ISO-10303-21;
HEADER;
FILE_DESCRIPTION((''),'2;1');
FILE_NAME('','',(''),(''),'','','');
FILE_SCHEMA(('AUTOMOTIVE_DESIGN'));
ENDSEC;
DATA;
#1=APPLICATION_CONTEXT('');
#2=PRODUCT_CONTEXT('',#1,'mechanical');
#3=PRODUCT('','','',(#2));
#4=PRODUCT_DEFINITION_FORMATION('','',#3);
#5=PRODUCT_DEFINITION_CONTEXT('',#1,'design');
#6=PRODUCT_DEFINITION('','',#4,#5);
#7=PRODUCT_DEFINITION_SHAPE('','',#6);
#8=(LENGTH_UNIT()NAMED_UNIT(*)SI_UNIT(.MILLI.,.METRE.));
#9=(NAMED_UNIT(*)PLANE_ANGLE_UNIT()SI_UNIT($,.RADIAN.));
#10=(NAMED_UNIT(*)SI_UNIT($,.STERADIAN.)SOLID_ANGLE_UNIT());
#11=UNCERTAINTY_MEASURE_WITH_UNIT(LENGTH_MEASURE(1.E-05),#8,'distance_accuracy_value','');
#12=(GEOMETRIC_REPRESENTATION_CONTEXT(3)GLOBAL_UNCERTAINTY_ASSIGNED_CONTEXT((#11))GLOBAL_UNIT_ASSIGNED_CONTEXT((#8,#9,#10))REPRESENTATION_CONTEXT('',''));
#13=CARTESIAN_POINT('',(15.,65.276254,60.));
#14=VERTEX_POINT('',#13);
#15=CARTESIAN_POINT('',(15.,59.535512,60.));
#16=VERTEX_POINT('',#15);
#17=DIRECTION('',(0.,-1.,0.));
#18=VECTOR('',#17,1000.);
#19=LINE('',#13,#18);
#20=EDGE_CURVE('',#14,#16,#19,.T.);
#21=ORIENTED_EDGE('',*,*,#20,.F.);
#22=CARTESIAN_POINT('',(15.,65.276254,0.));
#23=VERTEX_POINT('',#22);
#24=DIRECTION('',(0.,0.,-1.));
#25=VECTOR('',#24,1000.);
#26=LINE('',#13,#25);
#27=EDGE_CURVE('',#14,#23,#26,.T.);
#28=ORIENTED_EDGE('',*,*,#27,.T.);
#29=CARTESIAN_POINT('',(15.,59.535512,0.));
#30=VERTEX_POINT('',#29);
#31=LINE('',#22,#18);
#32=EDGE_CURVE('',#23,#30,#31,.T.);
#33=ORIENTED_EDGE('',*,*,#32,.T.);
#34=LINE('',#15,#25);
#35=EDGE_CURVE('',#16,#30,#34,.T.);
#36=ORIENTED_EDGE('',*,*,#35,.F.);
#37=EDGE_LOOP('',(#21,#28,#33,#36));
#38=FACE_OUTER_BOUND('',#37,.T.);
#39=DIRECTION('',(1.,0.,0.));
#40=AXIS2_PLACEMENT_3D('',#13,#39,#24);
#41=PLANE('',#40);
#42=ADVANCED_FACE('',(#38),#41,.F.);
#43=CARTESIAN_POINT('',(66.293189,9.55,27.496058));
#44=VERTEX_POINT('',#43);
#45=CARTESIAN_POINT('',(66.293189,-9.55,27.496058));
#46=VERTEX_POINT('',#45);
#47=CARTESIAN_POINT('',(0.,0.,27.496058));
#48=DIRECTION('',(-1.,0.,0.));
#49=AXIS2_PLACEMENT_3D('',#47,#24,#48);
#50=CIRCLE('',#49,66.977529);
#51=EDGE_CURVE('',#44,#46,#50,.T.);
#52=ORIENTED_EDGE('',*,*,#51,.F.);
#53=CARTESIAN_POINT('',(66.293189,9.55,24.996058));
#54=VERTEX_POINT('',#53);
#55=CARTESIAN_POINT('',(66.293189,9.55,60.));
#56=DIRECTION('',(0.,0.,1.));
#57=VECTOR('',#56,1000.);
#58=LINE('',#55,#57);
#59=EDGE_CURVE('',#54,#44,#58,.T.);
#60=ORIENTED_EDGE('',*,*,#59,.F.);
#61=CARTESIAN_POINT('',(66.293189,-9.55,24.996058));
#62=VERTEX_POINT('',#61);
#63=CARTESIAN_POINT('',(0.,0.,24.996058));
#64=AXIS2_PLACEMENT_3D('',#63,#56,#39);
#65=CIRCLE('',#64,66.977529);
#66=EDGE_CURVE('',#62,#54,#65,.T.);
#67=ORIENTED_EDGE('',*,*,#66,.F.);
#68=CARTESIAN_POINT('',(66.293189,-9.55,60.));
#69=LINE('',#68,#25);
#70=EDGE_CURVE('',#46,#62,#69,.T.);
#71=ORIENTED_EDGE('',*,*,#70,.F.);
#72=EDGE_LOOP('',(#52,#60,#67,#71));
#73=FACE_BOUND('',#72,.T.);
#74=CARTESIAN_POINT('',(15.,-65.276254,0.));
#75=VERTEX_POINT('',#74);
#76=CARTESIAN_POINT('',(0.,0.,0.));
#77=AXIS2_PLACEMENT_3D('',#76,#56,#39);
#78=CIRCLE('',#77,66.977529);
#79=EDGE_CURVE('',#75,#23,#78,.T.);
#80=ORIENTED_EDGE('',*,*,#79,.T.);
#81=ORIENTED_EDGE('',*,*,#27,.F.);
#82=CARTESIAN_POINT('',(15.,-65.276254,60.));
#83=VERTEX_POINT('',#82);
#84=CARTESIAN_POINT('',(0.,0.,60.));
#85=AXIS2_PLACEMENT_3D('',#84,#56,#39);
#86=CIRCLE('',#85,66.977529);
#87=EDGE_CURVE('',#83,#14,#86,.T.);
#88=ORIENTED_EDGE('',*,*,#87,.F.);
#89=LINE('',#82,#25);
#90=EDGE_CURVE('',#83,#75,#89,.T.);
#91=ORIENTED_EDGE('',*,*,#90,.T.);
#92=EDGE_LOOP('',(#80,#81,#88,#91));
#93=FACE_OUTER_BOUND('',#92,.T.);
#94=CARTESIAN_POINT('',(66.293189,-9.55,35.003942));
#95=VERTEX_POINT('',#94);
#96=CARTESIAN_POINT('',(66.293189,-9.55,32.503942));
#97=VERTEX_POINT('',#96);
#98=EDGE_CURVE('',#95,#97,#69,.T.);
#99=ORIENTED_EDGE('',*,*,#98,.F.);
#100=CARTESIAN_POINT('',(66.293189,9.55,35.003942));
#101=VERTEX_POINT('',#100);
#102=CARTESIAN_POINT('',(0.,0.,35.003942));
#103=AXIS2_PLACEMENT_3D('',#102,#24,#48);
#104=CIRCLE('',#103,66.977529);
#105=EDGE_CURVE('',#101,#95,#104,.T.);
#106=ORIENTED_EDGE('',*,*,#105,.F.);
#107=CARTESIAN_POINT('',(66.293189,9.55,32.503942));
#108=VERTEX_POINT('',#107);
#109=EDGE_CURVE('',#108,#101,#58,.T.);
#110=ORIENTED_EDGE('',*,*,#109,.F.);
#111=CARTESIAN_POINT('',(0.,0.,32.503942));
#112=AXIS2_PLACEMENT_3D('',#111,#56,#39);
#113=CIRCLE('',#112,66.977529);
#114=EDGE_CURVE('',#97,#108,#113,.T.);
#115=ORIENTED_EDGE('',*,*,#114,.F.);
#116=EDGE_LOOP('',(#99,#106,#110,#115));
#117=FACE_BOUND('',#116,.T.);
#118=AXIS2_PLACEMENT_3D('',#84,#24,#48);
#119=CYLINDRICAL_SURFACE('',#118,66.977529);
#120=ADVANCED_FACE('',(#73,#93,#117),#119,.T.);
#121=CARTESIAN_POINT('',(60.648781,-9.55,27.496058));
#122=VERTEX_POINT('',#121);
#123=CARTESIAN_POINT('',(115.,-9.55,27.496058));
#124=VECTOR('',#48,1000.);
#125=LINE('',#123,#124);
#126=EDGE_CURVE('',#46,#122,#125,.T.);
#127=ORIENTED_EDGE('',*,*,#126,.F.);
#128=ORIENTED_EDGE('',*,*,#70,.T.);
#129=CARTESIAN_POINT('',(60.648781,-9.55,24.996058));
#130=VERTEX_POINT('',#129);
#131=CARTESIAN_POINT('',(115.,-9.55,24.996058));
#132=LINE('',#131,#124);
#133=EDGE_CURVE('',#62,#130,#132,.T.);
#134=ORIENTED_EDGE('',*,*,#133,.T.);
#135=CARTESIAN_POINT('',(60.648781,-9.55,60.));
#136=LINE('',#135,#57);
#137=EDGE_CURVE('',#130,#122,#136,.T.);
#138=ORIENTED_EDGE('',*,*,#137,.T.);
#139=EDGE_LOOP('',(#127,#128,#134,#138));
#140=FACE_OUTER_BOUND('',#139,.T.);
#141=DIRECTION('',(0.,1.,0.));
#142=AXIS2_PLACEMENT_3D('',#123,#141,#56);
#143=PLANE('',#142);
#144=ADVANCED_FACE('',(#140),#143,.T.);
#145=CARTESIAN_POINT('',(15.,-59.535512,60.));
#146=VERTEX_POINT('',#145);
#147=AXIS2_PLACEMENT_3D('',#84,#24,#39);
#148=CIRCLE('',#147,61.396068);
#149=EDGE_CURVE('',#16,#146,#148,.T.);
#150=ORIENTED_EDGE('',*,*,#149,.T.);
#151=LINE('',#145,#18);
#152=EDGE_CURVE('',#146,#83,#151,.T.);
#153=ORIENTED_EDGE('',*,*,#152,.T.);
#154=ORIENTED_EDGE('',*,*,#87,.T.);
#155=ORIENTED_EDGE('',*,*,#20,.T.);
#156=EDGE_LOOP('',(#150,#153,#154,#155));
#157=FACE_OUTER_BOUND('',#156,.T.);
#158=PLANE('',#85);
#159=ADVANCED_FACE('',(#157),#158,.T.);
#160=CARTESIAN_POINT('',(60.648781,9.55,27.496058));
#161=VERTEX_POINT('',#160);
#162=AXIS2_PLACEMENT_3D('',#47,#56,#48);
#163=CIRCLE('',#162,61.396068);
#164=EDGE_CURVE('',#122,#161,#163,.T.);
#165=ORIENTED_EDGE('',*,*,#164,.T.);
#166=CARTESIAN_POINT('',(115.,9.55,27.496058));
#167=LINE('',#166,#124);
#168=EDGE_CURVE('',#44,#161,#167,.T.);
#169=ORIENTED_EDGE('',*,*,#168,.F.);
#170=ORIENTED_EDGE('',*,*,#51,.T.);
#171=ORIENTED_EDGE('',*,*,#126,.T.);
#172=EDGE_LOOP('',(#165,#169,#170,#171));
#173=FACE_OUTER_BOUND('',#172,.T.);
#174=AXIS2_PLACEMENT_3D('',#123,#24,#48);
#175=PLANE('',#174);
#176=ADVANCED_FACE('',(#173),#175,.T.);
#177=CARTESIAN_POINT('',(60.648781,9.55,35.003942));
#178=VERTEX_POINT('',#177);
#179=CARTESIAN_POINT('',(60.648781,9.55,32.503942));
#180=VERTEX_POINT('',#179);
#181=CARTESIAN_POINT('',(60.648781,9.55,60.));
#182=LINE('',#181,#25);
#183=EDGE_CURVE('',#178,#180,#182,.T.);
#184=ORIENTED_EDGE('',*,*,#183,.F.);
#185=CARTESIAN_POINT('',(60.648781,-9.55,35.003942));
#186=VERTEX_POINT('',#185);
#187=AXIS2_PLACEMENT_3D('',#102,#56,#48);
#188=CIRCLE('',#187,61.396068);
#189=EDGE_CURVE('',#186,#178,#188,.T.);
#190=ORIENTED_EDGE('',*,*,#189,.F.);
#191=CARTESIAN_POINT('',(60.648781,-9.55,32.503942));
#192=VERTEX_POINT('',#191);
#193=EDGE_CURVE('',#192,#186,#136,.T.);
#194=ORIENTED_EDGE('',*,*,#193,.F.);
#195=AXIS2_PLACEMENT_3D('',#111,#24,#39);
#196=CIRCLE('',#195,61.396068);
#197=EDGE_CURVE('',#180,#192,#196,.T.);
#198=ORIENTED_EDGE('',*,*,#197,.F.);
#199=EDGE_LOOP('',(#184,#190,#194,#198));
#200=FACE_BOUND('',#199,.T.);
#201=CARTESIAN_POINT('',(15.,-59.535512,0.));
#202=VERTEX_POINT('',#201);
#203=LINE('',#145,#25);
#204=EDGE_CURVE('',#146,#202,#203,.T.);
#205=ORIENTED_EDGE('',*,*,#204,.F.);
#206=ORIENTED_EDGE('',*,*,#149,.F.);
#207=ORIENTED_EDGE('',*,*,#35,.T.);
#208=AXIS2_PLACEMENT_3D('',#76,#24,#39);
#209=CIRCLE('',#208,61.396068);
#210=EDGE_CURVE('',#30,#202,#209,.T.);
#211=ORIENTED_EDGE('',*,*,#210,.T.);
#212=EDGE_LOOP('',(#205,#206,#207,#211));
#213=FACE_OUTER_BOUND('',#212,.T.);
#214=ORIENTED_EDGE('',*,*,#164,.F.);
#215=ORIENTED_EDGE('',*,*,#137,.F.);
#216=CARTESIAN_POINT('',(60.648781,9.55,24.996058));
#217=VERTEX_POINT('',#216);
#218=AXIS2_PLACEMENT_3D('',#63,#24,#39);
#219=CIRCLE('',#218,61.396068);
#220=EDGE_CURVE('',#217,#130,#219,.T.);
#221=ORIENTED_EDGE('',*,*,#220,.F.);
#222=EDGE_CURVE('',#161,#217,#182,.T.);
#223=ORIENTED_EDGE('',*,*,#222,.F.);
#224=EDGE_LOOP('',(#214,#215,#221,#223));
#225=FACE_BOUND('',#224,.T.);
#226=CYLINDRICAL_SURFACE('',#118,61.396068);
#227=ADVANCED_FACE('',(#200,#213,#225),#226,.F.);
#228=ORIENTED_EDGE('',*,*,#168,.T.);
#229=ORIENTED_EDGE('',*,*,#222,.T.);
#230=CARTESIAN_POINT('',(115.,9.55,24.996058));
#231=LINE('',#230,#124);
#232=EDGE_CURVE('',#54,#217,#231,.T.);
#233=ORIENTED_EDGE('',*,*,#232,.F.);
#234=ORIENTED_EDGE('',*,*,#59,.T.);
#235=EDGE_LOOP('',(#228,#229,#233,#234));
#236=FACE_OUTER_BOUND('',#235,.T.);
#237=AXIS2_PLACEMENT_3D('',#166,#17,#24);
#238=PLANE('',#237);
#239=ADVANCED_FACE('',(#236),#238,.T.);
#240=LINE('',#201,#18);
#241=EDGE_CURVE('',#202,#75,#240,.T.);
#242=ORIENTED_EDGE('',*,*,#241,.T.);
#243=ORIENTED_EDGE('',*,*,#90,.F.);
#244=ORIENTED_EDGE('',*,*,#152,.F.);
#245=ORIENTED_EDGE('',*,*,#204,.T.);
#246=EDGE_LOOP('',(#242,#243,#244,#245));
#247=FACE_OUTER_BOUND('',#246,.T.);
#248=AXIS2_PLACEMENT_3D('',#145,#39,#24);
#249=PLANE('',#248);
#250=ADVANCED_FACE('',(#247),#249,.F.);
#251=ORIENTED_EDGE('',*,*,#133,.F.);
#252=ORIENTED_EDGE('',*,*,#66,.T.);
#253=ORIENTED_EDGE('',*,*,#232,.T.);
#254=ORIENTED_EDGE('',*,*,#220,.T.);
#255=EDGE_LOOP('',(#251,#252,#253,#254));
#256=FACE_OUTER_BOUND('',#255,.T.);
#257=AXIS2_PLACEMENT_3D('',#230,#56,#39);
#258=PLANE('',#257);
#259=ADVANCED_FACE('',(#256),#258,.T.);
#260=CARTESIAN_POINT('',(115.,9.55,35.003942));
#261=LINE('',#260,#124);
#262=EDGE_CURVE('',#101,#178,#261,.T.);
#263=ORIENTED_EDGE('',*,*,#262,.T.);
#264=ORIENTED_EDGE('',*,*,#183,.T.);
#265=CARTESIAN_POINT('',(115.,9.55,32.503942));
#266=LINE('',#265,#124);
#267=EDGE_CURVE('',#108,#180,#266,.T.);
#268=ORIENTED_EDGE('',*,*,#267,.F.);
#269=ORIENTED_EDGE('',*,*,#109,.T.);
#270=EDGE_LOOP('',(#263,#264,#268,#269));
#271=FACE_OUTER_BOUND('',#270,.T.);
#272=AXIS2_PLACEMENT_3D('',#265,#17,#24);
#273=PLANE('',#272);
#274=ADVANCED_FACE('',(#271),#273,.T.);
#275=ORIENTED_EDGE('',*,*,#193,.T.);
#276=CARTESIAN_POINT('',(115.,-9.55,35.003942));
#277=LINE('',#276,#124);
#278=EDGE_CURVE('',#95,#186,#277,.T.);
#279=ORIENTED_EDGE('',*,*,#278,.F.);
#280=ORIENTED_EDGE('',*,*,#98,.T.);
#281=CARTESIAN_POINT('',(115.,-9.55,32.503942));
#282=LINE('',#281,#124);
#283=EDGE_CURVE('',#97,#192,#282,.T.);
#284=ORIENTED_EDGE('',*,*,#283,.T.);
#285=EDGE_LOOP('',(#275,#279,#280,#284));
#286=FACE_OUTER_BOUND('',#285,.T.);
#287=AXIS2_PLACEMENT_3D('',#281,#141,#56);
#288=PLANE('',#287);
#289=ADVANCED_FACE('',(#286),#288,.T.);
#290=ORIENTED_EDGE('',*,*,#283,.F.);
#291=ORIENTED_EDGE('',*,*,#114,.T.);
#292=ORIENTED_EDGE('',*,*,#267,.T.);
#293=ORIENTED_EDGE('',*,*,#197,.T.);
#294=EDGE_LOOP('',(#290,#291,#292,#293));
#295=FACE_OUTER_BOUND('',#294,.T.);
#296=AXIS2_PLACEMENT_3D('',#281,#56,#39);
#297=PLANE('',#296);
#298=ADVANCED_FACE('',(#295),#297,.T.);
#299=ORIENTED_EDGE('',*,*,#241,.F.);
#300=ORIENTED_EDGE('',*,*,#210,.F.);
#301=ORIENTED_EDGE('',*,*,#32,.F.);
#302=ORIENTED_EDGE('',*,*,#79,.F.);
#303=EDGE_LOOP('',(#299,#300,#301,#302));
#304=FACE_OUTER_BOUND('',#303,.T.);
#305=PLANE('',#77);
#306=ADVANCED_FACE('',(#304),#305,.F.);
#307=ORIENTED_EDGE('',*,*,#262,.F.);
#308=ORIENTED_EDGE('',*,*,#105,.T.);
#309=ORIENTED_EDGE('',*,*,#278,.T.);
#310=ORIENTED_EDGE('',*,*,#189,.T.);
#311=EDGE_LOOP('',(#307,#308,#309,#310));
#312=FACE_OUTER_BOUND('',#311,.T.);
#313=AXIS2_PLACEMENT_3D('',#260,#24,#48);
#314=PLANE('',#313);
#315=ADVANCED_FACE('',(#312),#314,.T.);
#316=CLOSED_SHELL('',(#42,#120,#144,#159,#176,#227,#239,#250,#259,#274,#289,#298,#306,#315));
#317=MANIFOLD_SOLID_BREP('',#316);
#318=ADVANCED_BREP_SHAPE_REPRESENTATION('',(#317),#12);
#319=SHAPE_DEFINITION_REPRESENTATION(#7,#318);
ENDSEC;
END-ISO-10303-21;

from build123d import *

# Parameters (mm, degrees)
EXTRUDE_1_DEPTH     = 60
SKETCH_3_W          = 2.5
SKETCH_3_H          = 19.1
CUT_EXTRUDE_2_DEPTH = 115


with BuildPart() as part:
    # 草图1 → 凸台-拉伸1 (new body)
    with BuildSketch(Plane.XY):
        with BuildLine():
            Line((15, 65.276254084), (15, 59.535511754))
            ThreePointArc((15, 59.535511754), (61.396067951, 0), (15, -59.535511754))
            Line((15, -59.535511754), (15, -65.276254084))
            ThreePointArc((15, -65.276254084), (66.977528674, 0), (15, 65.276254084))
        make_face()
    extrude(amount=EXTRUDE_1_DEPTH)

    # 草图3 → 切除-拉伸2 (cut)
    with BuildSketch(Plane(origin=(0, 0, 0), x_dir=(0, 0, -1), z_dir=(1, 0, 0))):
        with Locations((-33.75394201, 0)):
            Rectangle(SKETCH_3_W, SKETCH_3_H)
        with Locations((-26.24605799, 0)):
            Rectangle(SKETCH_3_W, SKETCH_3_H)
    extrude(amount=CUT_EXTRUDE_2_DEPTH, mode=Mode.SUBTRACT)


solid = part.part
